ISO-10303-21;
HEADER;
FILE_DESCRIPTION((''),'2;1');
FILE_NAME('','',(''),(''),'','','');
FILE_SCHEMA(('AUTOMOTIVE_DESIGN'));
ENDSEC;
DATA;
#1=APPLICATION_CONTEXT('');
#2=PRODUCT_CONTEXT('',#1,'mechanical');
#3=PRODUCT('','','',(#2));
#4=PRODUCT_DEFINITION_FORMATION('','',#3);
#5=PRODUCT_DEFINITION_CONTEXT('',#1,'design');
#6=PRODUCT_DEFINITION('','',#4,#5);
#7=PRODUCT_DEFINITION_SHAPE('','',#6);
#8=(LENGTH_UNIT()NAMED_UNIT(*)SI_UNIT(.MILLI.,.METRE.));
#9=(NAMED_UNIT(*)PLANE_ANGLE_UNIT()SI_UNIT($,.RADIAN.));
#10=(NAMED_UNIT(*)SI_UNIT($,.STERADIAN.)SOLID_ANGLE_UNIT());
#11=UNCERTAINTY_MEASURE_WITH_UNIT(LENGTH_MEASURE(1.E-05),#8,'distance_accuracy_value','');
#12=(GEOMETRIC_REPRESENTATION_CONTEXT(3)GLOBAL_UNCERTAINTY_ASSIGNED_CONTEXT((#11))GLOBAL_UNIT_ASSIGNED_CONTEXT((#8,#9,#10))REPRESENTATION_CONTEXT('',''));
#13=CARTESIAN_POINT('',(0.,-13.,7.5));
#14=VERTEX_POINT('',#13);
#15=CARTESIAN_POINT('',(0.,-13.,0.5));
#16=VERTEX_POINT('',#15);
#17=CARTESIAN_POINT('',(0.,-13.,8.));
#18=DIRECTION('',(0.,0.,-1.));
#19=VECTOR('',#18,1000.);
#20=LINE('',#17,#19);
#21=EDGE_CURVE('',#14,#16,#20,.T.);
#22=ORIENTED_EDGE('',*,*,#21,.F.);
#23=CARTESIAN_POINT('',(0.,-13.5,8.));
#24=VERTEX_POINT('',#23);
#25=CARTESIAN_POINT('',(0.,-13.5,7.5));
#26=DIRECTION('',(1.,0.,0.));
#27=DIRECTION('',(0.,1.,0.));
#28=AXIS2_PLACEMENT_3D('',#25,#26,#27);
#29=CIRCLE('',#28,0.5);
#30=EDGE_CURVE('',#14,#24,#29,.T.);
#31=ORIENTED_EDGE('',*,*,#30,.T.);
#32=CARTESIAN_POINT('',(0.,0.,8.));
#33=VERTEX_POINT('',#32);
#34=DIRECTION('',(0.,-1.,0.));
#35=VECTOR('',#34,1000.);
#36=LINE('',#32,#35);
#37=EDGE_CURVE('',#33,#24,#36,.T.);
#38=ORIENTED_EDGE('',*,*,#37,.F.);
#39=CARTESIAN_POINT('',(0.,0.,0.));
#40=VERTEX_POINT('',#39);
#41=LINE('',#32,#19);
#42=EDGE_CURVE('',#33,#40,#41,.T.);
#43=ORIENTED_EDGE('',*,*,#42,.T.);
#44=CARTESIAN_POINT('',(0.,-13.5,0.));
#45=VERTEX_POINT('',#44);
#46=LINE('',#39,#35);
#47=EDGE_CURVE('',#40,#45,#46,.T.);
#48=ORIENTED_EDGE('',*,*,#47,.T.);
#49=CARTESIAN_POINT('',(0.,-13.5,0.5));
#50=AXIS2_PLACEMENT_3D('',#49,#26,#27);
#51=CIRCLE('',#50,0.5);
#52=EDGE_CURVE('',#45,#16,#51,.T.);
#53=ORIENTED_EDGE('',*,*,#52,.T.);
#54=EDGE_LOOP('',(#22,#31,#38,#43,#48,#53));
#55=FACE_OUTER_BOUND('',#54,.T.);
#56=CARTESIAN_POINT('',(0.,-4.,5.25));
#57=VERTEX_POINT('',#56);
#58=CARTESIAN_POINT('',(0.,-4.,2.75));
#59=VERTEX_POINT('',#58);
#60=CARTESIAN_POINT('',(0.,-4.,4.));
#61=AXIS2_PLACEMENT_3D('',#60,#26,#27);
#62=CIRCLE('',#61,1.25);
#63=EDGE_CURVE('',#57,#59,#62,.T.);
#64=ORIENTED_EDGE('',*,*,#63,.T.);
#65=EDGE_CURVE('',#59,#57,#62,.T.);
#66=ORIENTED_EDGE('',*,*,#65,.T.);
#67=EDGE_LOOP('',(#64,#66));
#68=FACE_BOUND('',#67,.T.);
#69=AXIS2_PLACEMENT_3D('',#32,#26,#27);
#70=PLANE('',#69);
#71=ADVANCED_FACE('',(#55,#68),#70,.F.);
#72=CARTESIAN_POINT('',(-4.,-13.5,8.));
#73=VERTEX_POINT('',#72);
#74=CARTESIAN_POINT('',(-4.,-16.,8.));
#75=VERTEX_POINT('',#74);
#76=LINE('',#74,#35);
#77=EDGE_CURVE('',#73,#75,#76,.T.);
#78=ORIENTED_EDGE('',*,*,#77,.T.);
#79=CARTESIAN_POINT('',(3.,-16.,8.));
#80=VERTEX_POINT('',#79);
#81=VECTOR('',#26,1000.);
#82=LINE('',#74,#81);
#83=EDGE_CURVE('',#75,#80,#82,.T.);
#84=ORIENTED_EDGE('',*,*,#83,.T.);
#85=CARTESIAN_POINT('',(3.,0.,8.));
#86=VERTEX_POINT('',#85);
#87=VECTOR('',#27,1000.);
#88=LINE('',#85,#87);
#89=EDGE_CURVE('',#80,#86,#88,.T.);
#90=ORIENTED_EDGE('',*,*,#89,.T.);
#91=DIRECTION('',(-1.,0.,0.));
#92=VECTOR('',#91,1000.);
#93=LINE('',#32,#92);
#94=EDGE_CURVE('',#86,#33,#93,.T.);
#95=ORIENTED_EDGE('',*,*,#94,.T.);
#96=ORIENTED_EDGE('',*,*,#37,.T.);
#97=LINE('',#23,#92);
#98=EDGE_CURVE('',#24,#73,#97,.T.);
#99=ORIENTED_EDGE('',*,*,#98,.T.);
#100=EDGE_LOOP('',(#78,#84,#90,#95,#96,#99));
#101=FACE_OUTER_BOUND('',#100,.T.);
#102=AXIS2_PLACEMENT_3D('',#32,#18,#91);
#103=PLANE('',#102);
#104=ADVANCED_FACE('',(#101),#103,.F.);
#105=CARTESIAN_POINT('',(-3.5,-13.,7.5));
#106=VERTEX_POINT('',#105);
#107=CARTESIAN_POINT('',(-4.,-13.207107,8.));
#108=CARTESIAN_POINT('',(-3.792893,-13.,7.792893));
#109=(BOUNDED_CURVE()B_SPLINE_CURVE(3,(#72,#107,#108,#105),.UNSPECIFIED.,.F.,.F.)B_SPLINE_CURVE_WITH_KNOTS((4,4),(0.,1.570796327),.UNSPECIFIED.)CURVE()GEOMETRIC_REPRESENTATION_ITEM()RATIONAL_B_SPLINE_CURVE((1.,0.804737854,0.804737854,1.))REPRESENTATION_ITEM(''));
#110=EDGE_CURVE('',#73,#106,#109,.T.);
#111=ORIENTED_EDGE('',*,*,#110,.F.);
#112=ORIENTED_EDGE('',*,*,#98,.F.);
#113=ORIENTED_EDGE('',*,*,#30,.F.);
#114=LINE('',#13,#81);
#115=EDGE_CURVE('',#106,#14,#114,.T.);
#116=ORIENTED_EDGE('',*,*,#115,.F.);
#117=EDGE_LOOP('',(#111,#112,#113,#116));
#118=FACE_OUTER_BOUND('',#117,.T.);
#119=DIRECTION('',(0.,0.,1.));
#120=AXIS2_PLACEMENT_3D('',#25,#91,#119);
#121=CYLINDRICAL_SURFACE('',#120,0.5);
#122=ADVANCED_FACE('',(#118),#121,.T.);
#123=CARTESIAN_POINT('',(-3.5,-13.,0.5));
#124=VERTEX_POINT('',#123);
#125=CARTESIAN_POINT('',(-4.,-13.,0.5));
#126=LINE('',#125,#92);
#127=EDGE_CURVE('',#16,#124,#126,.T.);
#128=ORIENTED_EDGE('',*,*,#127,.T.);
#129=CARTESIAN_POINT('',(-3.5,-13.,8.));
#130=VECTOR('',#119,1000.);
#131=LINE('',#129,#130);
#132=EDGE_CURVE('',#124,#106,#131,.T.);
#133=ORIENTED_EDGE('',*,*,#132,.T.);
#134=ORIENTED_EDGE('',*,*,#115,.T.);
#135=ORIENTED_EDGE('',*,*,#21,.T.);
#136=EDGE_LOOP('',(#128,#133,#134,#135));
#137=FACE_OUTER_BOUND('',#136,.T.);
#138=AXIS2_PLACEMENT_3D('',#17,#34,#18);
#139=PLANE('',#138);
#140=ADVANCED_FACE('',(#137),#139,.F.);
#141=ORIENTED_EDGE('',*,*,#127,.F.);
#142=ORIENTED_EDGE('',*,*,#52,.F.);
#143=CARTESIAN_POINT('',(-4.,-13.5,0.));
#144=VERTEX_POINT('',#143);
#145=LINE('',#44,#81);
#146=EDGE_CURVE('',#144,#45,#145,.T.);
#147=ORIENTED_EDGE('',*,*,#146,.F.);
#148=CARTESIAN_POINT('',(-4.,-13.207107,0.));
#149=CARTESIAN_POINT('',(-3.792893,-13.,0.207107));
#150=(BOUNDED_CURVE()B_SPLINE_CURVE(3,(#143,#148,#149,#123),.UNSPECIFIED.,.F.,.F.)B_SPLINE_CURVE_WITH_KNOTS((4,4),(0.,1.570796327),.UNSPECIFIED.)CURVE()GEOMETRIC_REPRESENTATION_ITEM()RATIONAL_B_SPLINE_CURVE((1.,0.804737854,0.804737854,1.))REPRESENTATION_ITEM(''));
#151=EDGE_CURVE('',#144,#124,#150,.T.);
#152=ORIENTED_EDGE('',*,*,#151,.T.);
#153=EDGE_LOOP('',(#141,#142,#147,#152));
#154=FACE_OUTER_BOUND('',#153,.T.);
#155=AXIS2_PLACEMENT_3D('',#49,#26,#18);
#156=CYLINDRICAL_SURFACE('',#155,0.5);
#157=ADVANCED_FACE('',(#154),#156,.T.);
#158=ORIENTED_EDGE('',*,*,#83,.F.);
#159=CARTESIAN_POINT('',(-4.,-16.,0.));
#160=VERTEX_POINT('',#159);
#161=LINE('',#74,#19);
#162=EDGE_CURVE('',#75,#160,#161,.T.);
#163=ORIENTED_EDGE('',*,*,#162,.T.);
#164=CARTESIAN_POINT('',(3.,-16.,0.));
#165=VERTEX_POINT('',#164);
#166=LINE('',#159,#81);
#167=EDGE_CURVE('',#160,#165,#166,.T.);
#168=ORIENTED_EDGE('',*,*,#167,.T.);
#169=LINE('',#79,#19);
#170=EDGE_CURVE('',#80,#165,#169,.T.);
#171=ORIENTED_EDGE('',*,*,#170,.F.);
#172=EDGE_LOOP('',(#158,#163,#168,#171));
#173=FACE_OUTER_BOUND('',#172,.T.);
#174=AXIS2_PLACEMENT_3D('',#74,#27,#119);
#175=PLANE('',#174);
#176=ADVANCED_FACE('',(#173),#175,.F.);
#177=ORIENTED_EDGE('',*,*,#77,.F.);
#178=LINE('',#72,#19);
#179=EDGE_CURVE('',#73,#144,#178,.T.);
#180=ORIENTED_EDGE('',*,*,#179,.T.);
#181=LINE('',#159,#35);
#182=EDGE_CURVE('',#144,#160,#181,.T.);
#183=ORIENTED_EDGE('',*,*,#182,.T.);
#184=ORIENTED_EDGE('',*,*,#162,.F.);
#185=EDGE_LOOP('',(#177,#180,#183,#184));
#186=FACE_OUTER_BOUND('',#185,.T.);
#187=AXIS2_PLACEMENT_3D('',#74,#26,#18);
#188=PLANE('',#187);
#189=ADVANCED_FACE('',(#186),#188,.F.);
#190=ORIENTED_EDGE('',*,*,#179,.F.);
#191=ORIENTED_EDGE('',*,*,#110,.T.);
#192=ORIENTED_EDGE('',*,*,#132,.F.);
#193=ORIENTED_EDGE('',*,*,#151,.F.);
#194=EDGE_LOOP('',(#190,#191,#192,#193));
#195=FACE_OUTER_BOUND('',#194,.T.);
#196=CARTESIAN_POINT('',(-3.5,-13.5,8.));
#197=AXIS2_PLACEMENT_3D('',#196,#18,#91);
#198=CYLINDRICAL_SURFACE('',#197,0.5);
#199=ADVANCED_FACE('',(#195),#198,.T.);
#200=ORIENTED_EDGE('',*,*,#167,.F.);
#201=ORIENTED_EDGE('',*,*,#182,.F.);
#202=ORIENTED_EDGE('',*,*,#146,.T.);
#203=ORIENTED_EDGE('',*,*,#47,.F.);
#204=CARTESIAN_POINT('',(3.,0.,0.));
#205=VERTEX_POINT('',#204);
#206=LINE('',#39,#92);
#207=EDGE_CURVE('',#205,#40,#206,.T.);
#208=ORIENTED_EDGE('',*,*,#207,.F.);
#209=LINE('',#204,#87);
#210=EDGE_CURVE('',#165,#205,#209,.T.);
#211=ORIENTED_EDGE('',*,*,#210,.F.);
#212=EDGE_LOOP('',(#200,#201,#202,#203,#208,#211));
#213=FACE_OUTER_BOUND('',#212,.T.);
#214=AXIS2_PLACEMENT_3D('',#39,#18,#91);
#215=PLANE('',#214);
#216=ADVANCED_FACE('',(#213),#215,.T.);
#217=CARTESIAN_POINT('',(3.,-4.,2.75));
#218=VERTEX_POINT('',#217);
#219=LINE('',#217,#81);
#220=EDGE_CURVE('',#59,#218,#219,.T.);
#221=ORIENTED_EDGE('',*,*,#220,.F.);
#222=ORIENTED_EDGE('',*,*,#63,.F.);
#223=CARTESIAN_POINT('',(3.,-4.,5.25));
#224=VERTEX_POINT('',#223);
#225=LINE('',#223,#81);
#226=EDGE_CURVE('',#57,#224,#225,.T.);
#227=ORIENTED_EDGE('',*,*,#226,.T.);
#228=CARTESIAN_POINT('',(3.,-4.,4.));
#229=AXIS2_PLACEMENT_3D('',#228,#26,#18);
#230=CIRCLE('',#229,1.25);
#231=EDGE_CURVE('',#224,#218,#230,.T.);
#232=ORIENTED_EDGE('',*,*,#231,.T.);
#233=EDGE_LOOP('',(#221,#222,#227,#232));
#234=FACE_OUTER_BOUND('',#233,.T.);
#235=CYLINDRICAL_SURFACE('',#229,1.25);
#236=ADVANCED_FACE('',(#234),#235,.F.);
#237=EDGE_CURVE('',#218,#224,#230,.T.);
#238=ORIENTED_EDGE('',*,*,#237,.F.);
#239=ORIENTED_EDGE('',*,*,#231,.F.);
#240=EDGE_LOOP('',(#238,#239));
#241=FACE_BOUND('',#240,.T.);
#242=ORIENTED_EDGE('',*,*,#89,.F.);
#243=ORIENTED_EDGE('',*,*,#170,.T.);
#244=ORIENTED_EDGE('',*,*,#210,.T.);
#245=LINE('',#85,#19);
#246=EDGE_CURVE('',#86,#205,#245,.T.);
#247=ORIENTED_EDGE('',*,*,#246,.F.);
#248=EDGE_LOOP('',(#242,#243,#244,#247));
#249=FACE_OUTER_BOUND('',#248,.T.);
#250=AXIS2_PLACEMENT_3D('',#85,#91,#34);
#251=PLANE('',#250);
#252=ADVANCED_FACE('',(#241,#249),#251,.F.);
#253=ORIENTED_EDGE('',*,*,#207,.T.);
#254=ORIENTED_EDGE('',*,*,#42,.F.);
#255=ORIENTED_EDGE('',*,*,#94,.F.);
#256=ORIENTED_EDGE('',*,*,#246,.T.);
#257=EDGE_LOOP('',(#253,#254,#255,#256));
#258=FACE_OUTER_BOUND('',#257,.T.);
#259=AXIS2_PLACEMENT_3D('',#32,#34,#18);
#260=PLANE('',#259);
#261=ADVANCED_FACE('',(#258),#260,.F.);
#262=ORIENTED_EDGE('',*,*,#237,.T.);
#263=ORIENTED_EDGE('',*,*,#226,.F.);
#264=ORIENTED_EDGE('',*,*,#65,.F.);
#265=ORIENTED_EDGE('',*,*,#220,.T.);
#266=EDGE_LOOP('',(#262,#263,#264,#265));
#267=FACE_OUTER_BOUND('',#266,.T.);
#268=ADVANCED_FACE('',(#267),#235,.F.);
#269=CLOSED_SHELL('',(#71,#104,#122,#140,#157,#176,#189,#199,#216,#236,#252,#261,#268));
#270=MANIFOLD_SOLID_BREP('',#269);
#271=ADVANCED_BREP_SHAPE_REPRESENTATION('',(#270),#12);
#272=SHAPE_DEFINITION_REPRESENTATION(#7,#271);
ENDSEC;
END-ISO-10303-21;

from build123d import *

# Parameters (mm, degrees)
EXTRUDE_1_DEPTH    = 8
HOLE_WIZARD_M3_1_D = 2.5
FILLET_1_R         = 0.5


with BuildPart() as part:
    # 草图1 → 凸台-拉伸1 (new body)
    with BuildSketch(Plane.XY):
        Polygon((-4, -16), (3, -16), (3, 0), (0, 0), (0, -13), (-4, -13), align=None)
    extrude(amount=EXTRUDE_1_DEPTH)

    # M3 螺纹孔1 (through all)
    with Locations(Plane(origin=(3, 0, 0), x_dir=(0, 0, -1), z_dir=(1, 0, 0))):
        with Locations((-4, -4)):
            Hole(HOLE_WIZARD_M3_1_D / 2)

    # 圆角1
    fillet_1_edges = [part.edges().sort_by_distance(p)[0] for p in [
        (-4, -13, 4),
        (-2, -13, 8),
        (-2, -13, 0),
    ]]
    fillet(fillet_1_edges, radius=FILLET_1_R)


solid = part.part
